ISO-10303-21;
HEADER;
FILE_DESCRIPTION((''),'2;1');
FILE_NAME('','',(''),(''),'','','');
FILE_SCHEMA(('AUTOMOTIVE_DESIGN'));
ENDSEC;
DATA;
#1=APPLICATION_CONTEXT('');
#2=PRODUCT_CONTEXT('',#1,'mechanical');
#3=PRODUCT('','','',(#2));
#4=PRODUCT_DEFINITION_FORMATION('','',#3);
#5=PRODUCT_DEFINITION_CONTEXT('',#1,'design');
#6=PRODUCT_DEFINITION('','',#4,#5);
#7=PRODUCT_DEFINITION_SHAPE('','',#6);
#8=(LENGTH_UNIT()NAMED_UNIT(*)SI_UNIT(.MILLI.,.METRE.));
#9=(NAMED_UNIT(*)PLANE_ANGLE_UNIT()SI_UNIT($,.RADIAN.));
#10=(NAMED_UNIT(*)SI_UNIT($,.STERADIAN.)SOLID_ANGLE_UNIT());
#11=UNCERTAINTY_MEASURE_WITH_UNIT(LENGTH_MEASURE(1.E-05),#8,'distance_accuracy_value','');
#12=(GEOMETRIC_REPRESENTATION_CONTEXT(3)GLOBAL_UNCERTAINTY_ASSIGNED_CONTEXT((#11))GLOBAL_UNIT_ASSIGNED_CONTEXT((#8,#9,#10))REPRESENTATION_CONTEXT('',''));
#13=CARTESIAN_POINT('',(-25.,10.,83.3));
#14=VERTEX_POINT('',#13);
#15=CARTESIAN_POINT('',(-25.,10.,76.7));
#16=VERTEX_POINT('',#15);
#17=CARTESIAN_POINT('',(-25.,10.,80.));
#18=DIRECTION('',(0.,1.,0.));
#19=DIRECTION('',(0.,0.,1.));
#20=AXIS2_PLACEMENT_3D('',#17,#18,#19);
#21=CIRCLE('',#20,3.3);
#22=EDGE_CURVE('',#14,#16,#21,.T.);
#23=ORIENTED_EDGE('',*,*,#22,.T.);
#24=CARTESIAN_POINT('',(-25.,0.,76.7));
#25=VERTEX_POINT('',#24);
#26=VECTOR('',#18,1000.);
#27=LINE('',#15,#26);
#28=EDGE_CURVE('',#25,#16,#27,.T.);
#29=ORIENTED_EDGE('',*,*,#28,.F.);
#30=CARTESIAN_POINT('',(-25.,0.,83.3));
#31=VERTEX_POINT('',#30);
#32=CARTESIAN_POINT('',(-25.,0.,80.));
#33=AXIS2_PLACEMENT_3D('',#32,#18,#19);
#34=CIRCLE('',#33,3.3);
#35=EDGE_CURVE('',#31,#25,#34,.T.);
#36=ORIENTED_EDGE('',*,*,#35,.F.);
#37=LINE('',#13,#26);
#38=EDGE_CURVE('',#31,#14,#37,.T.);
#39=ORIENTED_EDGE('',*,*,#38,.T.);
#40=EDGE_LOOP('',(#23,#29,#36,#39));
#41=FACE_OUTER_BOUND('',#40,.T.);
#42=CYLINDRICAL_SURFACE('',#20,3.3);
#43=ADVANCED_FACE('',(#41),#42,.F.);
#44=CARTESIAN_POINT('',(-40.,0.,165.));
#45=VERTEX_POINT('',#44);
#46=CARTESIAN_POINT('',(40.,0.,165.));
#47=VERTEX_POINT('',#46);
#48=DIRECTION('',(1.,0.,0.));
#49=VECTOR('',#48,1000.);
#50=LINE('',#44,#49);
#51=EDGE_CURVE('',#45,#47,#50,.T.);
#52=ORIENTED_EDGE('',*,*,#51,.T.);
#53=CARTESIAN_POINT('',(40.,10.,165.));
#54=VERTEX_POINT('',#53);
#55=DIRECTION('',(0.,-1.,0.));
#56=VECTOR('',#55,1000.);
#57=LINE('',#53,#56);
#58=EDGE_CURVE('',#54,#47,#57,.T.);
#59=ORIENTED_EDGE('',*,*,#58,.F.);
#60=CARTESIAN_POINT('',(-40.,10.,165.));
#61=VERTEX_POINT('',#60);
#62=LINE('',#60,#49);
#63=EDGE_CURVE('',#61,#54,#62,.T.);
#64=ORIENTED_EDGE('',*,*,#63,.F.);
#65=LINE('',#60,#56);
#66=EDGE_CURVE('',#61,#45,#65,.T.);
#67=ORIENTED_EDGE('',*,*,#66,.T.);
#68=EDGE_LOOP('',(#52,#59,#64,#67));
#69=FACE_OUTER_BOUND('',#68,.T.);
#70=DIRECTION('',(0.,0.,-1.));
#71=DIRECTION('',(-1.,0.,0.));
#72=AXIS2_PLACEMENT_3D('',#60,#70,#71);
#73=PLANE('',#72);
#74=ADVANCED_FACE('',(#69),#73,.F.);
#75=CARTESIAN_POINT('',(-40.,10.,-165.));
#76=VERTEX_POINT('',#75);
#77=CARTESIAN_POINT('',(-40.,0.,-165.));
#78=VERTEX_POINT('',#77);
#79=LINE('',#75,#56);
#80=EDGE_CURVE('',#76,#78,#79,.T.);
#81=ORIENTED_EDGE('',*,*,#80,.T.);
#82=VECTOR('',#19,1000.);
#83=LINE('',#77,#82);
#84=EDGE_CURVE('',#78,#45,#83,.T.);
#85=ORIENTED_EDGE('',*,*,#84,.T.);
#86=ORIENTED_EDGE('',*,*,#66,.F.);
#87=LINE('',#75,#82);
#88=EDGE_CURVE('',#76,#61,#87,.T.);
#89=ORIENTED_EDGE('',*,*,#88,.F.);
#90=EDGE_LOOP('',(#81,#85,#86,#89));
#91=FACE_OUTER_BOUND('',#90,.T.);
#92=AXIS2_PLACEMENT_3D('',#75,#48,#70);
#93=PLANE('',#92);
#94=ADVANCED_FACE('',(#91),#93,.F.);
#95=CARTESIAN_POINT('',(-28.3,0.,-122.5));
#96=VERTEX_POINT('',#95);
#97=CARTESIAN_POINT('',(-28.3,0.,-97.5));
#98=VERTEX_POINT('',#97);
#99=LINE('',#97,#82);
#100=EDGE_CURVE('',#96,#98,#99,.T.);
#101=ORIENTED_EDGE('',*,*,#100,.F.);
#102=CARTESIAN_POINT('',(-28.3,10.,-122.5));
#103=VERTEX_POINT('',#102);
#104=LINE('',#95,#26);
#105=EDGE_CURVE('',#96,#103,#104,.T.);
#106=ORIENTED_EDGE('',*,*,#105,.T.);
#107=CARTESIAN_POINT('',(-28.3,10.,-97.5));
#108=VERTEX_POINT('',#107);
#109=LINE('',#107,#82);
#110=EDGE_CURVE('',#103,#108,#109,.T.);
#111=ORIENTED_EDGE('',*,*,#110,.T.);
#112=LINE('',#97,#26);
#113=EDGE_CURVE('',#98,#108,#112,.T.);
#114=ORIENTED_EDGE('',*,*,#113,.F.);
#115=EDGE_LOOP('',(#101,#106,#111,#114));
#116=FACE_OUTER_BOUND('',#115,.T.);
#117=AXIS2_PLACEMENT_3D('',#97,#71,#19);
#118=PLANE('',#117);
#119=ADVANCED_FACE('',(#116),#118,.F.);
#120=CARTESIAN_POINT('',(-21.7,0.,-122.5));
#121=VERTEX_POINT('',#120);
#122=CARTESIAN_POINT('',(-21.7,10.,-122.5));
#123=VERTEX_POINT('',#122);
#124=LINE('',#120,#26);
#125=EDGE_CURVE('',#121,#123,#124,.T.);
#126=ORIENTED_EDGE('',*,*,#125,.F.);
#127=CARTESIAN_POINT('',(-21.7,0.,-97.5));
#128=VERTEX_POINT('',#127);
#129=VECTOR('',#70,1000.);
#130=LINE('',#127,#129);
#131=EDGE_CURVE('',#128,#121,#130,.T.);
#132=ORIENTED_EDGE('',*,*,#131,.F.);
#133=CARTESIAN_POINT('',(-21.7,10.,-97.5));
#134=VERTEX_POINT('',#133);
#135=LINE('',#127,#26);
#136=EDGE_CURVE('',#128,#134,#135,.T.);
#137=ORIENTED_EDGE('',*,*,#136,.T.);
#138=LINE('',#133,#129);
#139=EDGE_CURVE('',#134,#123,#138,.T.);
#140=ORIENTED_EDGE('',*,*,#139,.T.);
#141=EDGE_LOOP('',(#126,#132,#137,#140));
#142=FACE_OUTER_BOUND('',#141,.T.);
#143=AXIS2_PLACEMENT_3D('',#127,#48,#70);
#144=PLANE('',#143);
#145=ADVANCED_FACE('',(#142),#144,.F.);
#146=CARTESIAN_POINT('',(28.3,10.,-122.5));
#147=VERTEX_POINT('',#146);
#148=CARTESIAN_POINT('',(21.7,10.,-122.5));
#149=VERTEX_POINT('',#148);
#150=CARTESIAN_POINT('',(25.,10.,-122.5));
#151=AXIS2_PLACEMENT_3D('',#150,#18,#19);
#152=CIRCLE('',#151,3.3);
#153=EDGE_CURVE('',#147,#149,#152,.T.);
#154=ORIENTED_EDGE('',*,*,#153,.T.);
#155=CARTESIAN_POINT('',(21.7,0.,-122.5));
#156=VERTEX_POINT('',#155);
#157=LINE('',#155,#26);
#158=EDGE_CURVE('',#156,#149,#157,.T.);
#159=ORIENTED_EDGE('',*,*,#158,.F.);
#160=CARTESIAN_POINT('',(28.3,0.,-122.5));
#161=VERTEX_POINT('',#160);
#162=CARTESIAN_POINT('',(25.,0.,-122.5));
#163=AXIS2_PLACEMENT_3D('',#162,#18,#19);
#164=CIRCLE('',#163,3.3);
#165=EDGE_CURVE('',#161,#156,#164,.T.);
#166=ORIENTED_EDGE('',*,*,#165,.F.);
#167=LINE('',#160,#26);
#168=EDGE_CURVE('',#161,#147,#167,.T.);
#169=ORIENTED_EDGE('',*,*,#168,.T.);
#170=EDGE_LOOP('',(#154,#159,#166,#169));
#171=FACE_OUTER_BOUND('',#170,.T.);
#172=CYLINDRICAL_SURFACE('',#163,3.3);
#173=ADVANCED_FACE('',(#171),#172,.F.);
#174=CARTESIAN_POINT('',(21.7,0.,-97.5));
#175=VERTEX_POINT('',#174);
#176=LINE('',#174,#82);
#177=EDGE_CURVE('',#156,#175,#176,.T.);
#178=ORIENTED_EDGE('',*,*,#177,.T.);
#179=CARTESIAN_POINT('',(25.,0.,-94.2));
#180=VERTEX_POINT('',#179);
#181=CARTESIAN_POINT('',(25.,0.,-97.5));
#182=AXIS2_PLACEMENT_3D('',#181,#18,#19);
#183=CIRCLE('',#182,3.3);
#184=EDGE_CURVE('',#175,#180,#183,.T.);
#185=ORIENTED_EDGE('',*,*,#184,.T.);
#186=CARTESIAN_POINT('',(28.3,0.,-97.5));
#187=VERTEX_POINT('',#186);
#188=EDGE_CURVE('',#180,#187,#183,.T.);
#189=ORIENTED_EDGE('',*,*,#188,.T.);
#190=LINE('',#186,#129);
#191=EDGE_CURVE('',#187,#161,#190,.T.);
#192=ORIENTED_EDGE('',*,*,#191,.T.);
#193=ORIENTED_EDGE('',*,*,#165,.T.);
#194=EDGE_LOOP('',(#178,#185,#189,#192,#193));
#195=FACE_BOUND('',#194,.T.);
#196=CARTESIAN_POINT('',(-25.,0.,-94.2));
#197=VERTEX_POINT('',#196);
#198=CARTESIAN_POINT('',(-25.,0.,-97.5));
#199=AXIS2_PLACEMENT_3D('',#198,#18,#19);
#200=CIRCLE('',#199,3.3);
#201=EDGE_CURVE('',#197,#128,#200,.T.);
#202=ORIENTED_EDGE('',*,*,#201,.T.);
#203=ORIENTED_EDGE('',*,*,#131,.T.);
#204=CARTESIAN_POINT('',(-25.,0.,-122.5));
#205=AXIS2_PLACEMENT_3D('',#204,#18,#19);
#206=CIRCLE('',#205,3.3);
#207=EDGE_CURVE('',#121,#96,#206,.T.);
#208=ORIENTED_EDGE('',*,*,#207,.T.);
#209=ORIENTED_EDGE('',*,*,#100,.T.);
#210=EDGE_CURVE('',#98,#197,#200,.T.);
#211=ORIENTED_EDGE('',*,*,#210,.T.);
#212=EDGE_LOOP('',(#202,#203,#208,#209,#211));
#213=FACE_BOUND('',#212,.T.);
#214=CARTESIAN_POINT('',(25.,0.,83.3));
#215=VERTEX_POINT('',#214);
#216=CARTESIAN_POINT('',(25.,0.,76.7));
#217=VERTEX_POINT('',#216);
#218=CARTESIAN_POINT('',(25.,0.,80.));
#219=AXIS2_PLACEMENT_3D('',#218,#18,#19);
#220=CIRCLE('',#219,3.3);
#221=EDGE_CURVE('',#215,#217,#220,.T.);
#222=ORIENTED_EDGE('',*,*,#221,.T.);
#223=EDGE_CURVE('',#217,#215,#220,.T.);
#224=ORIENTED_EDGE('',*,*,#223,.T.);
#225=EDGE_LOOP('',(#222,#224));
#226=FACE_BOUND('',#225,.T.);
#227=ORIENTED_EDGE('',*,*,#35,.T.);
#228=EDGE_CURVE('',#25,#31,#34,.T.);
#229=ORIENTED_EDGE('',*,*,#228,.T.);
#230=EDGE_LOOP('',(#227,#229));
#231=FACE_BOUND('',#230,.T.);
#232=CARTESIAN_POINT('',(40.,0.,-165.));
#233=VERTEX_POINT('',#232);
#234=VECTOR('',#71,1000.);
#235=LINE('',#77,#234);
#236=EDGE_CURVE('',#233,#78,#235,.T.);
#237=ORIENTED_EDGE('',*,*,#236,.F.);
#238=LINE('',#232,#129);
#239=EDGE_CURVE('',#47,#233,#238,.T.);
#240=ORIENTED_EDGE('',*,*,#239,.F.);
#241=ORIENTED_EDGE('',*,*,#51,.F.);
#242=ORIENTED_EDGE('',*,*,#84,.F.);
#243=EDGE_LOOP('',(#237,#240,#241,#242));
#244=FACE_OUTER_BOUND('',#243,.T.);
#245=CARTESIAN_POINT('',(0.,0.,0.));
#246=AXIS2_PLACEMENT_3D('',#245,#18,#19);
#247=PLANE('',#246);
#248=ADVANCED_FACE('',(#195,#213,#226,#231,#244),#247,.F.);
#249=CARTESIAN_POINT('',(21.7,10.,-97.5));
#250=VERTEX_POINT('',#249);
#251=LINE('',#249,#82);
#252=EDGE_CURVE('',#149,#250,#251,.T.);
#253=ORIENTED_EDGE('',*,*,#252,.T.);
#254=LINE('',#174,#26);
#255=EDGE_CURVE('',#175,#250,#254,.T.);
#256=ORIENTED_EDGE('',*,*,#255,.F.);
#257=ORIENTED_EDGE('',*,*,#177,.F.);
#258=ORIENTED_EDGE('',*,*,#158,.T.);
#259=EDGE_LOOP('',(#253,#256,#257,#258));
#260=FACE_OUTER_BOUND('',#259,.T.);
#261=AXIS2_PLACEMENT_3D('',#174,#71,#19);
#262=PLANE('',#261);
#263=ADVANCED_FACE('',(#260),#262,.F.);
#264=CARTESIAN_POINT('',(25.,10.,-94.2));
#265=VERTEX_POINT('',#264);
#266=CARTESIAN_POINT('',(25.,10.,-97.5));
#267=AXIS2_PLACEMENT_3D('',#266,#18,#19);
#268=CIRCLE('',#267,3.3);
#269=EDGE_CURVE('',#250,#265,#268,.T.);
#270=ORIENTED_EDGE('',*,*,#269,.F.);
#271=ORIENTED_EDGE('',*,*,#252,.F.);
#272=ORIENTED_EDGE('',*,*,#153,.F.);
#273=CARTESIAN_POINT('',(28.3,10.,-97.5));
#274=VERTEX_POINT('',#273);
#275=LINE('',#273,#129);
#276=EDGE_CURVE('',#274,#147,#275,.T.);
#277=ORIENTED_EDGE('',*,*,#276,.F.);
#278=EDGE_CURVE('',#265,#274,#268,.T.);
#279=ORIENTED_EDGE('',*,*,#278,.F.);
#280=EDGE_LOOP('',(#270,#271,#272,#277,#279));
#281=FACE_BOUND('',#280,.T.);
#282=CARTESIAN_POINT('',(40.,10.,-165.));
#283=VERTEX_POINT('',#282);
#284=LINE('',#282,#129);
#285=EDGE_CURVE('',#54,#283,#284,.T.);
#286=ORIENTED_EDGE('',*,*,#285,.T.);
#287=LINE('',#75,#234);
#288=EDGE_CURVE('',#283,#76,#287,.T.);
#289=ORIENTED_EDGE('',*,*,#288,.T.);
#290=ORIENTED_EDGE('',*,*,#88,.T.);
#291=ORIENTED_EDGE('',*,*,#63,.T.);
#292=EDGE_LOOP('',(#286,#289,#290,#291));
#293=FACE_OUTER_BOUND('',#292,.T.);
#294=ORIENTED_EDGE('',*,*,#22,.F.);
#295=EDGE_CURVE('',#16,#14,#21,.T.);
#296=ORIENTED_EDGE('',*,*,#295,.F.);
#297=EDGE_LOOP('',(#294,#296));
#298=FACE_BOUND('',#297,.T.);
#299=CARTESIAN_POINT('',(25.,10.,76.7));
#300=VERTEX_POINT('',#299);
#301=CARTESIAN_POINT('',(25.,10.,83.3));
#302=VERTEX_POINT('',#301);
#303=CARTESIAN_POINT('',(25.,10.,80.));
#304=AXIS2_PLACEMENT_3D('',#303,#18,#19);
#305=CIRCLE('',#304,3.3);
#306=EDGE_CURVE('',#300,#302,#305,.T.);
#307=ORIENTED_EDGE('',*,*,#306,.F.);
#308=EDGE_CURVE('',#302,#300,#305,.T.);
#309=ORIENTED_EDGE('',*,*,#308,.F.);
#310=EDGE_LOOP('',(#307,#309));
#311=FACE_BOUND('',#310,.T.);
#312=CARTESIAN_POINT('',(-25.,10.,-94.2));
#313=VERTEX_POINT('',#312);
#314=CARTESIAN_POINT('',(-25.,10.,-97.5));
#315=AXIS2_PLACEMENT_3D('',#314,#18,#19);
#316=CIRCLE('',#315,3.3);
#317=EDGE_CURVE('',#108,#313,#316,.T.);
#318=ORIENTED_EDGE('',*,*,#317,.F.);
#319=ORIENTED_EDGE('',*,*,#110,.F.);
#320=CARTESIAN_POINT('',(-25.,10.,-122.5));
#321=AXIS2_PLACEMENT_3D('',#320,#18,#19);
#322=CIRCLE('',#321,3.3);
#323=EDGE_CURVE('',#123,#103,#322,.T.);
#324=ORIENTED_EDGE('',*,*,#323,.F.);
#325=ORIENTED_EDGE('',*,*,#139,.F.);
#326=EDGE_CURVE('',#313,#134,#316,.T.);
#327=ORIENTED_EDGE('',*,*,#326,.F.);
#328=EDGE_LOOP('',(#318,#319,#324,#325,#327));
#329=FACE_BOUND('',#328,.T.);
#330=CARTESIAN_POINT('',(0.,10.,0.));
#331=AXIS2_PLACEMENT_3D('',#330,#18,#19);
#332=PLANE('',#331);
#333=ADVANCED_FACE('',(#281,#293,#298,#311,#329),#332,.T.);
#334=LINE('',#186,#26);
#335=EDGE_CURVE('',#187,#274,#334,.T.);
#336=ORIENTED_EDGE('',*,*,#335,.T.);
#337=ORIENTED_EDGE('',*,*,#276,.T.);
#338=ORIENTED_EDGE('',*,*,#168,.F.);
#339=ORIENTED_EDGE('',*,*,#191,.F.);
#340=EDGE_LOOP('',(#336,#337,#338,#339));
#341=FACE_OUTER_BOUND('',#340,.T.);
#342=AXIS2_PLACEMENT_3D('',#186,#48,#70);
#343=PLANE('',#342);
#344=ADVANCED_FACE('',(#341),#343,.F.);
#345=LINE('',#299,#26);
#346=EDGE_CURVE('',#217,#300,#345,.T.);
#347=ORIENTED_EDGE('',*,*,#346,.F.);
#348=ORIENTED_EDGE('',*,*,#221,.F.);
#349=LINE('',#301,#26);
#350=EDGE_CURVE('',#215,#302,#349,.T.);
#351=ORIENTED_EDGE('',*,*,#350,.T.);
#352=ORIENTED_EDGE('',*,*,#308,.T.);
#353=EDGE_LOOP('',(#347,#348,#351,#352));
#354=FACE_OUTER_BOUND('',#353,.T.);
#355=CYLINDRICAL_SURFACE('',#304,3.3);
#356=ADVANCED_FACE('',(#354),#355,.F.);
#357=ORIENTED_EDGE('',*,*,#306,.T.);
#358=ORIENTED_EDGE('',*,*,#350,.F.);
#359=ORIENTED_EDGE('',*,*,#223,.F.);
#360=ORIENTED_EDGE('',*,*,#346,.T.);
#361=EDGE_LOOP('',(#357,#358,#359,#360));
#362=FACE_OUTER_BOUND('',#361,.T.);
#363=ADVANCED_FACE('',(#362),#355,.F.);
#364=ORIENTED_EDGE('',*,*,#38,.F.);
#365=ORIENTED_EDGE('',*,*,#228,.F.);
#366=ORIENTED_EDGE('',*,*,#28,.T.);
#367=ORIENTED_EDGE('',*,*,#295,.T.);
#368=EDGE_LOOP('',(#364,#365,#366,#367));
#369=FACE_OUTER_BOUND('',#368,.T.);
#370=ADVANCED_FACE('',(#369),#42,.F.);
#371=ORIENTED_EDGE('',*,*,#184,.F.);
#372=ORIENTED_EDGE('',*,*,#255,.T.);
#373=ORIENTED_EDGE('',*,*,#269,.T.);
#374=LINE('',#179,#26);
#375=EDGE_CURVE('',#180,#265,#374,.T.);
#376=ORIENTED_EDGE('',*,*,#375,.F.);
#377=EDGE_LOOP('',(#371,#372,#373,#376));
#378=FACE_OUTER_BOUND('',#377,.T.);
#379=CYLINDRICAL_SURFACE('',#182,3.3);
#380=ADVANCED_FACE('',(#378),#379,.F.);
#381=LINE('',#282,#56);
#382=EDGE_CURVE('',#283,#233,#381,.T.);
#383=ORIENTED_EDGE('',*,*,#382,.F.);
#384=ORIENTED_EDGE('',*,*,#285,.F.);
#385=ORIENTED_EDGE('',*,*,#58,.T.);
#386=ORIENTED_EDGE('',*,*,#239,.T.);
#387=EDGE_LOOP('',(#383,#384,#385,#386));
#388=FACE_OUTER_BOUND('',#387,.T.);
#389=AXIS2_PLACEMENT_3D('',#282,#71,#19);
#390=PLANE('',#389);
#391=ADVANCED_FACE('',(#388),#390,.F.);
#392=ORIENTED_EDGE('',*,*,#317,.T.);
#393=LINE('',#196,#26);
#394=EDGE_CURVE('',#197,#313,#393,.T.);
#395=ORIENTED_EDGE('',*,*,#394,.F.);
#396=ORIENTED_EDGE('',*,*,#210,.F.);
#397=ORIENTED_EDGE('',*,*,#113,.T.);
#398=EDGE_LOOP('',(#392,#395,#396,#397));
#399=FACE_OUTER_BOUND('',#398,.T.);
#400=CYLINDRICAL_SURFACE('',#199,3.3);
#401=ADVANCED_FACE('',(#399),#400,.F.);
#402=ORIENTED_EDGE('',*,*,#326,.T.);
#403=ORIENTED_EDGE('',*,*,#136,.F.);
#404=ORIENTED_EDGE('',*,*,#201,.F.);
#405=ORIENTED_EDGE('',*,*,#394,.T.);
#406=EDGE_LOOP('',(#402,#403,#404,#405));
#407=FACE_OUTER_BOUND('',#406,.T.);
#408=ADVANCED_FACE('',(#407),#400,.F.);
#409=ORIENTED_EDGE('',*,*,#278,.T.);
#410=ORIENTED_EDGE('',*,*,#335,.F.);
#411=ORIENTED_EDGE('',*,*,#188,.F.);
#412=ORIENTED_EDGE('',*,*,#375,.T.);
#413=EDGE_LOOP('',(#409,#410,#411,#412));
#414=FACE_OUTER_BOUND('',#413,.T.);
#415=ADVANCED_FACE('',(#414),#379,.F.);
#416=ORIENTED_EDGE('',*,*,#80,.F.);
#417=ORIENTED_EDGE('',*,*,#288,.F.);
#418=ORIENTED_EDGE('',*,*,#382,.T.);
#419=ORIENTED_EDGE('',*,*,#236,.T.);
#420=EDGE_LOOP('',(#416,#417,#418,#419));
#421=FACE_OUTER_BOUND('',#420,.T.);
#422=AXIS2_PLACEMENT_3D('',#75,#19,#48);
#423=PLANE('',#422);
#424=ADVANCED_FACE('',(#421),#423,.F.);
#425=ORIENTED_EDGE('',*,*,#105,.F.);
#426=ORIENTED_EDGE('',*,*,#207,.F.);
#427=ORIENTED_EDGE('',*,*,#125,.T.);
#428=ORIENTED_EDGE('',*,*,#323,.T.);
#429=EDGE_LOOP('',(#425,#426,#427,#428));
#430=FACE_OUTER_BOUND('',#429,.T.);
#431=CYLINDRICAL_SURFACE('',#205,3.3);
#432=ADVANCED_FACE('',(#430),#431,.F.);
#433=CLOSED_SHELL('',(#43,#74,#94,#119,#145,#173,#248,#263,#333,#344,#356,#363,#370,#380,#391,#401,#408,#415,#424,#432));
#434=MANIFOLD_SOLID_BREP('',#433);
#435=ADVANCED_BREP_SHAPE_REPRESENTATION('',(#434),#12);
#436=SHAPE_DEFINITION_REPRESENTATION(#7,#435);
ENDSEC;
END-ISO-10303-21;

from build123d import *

# Parameters (mm, degrees)
SKETCH1_W                  = 80
SKETCH1_H                  = 330
BOSS_EXTRUDE1_DEPTH        = 10
F_6_6_6_6_DIAMETER_HOLE1_D = 6.6
CUT_EXTRUDE1_DEPTH         = 10


with BuildPart() as part:
    # Sketch1 → Boss-Extrude1 (new body)
    with BuildSketch(Plane(origin=(0, 0, 0), x_dir=(1, 0, 0), z_dir=(0, 1, 0))):
        Rectangle(SKETCH1_W, SKETCH1_H)
    extrude(amount=BOSS_EXTRUDE1_DEPTH)

    # Ø6.6 (6.6) Diameter Hole1 (through all)
    with Locations(Plane(origin=(0, 10, 0), x_dir=(1, 0, 0), z_dir=(0, 1, 0))):
        with Locations((-25, -80), (25, -80)):
            Hole(F_6_6_6_6_DIAMETER_HOLE1_D / 2)

    # Sketch5 → Cut-Extrude1 (cut)
    with BuildSketch(Plane(origin=(0, 10, 0), x_dir=(1, 0, 0), z_dir=(0, 1, 0))):
        with BuildLine():
            Line((-28.3, 97.5), (-28.3, 122.5))
            ThreePointArc((-28.3, 122.5), (-25, 125.8), (-21.7, 122.5))
            Line((-21.7, 122.5), (-21.7, 97.5))
            ThreePointArc((-21.7, 97.5), (-25, 94.2), (-28.3, 97.5))
        make_face()
        with BuildLine():
            Line((21.7, 97.5), (21.7, 122.5))
            ThreePointArc((21.7, 122.5), (25, 125.8), (28.3, 122.5))
            Line((28.3, 122.5), (28.3, 97.5))
            ThreePointArc((28.3, 97.5), (25, 94.2), (21.7, 97.5))
        make_face()
    extrude(amount=-CUT_EXTRUDE1_DEPTH, mode=Mode.SUBTRACT)


solid = part.part
